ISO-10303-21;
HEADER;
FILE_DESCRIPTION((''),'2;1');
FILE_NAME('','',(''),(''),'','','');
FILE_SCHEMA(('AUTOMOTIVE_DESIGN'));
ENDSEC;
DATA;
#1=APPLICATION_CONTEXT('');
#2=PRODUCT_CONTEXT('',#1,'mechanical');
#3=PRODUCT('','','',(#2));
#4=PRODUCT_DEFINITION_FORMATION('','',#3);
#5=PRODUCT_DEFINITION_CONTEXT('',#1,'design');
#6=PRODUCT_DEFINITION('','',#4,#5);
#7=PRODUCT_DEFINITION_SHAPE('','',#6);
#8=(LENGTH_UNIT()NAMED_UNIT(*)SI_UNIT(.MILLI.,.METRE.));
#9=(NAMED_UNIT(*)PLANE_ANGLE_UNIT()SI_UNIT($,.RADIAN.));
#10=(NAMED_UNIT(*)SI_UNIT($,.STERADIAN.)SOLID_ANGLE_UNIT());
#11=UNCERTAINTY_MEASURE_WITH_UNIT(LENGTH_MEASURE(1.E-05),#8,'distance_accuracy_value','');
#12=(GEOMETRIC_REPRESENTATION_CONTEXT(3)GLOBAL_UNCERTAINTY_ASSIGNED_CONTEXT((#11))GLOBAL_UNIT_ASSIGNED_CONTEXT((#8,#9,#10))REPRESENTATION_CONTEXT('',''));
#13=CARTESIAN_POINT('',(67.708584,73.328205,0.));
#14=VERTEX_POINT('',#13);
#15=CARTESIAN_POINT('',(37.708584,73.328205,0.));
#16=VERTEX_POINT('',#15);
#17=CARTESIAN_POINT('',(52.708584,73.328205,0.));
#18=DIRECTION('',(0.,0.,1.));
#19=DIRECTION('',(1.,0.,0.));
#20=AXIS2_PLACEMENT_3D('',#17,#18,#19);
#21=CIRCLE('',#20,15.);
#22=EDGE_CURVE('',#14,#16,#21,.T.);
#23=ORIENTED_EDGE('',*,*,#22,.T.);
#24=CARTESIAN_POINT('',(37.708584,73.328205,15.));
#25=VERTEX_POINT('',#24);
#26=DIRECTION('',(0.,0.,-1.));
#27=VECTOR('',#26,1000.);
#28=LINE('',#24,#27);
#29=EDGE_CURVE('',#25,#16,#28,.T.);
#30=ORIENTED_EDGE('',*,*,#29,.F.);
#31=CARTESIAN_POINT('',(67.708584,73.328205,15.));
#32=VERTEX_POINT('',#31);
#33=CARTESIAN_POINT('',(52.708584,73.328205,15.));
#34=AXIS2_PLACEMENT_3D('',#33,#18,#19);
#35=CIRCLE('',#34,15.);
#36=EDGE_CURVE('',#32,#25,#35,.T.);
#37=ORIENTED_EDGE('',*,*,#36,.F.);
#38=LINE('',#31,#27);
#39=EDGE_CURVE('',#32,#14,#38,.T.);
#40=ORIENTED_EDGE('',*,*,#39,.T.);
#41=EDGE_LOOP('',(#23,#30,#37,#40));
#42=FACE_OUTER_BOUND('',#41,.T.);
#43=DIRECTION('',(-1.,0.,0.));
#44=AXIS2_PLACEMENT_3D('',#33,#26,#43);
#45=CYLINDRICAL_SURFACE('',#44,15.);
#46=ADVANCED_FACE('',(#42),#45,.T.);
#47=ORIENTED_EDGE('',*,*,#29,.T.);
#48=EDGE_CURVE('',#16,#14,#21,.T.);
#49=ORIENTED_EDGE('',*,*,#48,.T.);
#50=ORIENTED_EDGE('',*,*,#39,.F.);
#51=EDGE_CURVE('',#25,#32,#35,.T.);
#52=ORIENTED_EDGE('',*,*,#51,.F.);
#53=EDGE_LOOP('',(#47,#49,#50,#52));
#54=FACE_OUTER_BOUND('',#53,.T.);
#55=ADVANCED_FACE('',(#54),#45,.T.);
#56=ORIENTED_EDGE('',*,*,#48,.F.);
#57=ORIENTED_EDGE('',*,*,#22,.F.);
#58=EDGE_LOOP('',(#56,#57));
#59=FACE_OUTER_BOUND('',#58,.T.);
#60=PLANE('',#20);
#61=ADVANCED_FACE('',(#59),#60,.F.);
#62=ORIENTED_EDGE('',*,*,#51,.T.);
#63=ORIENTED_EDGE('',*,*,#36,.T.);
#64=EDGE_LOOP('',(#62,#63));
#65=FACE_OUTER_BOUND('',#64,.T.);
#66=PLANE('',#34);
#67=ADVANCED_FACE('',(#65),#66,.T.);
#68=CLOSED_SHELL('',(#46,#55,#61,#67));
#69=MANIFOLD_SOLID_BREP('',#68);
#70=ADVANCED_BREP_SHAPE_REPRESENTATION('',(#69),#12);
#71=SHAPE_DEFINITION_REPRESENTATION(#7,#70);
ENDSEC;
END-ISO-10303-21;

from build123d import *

# Parameters (mm, degrees)
SKETCH1_R           = 15
BOSS_EXTRUDE1_DEPTH = 15


with BuildPart() as part:
    # Sketch1 → Boss-Extrude1 (new body)
    with BuildSketch(Plane.XY):
        with Locations((52.708583994, 73.328205372)):
            Circle(SKETCH1_R)
    extrude(amount=BOSS_EXTRUDE1_DEPTH)


solid = part.part
